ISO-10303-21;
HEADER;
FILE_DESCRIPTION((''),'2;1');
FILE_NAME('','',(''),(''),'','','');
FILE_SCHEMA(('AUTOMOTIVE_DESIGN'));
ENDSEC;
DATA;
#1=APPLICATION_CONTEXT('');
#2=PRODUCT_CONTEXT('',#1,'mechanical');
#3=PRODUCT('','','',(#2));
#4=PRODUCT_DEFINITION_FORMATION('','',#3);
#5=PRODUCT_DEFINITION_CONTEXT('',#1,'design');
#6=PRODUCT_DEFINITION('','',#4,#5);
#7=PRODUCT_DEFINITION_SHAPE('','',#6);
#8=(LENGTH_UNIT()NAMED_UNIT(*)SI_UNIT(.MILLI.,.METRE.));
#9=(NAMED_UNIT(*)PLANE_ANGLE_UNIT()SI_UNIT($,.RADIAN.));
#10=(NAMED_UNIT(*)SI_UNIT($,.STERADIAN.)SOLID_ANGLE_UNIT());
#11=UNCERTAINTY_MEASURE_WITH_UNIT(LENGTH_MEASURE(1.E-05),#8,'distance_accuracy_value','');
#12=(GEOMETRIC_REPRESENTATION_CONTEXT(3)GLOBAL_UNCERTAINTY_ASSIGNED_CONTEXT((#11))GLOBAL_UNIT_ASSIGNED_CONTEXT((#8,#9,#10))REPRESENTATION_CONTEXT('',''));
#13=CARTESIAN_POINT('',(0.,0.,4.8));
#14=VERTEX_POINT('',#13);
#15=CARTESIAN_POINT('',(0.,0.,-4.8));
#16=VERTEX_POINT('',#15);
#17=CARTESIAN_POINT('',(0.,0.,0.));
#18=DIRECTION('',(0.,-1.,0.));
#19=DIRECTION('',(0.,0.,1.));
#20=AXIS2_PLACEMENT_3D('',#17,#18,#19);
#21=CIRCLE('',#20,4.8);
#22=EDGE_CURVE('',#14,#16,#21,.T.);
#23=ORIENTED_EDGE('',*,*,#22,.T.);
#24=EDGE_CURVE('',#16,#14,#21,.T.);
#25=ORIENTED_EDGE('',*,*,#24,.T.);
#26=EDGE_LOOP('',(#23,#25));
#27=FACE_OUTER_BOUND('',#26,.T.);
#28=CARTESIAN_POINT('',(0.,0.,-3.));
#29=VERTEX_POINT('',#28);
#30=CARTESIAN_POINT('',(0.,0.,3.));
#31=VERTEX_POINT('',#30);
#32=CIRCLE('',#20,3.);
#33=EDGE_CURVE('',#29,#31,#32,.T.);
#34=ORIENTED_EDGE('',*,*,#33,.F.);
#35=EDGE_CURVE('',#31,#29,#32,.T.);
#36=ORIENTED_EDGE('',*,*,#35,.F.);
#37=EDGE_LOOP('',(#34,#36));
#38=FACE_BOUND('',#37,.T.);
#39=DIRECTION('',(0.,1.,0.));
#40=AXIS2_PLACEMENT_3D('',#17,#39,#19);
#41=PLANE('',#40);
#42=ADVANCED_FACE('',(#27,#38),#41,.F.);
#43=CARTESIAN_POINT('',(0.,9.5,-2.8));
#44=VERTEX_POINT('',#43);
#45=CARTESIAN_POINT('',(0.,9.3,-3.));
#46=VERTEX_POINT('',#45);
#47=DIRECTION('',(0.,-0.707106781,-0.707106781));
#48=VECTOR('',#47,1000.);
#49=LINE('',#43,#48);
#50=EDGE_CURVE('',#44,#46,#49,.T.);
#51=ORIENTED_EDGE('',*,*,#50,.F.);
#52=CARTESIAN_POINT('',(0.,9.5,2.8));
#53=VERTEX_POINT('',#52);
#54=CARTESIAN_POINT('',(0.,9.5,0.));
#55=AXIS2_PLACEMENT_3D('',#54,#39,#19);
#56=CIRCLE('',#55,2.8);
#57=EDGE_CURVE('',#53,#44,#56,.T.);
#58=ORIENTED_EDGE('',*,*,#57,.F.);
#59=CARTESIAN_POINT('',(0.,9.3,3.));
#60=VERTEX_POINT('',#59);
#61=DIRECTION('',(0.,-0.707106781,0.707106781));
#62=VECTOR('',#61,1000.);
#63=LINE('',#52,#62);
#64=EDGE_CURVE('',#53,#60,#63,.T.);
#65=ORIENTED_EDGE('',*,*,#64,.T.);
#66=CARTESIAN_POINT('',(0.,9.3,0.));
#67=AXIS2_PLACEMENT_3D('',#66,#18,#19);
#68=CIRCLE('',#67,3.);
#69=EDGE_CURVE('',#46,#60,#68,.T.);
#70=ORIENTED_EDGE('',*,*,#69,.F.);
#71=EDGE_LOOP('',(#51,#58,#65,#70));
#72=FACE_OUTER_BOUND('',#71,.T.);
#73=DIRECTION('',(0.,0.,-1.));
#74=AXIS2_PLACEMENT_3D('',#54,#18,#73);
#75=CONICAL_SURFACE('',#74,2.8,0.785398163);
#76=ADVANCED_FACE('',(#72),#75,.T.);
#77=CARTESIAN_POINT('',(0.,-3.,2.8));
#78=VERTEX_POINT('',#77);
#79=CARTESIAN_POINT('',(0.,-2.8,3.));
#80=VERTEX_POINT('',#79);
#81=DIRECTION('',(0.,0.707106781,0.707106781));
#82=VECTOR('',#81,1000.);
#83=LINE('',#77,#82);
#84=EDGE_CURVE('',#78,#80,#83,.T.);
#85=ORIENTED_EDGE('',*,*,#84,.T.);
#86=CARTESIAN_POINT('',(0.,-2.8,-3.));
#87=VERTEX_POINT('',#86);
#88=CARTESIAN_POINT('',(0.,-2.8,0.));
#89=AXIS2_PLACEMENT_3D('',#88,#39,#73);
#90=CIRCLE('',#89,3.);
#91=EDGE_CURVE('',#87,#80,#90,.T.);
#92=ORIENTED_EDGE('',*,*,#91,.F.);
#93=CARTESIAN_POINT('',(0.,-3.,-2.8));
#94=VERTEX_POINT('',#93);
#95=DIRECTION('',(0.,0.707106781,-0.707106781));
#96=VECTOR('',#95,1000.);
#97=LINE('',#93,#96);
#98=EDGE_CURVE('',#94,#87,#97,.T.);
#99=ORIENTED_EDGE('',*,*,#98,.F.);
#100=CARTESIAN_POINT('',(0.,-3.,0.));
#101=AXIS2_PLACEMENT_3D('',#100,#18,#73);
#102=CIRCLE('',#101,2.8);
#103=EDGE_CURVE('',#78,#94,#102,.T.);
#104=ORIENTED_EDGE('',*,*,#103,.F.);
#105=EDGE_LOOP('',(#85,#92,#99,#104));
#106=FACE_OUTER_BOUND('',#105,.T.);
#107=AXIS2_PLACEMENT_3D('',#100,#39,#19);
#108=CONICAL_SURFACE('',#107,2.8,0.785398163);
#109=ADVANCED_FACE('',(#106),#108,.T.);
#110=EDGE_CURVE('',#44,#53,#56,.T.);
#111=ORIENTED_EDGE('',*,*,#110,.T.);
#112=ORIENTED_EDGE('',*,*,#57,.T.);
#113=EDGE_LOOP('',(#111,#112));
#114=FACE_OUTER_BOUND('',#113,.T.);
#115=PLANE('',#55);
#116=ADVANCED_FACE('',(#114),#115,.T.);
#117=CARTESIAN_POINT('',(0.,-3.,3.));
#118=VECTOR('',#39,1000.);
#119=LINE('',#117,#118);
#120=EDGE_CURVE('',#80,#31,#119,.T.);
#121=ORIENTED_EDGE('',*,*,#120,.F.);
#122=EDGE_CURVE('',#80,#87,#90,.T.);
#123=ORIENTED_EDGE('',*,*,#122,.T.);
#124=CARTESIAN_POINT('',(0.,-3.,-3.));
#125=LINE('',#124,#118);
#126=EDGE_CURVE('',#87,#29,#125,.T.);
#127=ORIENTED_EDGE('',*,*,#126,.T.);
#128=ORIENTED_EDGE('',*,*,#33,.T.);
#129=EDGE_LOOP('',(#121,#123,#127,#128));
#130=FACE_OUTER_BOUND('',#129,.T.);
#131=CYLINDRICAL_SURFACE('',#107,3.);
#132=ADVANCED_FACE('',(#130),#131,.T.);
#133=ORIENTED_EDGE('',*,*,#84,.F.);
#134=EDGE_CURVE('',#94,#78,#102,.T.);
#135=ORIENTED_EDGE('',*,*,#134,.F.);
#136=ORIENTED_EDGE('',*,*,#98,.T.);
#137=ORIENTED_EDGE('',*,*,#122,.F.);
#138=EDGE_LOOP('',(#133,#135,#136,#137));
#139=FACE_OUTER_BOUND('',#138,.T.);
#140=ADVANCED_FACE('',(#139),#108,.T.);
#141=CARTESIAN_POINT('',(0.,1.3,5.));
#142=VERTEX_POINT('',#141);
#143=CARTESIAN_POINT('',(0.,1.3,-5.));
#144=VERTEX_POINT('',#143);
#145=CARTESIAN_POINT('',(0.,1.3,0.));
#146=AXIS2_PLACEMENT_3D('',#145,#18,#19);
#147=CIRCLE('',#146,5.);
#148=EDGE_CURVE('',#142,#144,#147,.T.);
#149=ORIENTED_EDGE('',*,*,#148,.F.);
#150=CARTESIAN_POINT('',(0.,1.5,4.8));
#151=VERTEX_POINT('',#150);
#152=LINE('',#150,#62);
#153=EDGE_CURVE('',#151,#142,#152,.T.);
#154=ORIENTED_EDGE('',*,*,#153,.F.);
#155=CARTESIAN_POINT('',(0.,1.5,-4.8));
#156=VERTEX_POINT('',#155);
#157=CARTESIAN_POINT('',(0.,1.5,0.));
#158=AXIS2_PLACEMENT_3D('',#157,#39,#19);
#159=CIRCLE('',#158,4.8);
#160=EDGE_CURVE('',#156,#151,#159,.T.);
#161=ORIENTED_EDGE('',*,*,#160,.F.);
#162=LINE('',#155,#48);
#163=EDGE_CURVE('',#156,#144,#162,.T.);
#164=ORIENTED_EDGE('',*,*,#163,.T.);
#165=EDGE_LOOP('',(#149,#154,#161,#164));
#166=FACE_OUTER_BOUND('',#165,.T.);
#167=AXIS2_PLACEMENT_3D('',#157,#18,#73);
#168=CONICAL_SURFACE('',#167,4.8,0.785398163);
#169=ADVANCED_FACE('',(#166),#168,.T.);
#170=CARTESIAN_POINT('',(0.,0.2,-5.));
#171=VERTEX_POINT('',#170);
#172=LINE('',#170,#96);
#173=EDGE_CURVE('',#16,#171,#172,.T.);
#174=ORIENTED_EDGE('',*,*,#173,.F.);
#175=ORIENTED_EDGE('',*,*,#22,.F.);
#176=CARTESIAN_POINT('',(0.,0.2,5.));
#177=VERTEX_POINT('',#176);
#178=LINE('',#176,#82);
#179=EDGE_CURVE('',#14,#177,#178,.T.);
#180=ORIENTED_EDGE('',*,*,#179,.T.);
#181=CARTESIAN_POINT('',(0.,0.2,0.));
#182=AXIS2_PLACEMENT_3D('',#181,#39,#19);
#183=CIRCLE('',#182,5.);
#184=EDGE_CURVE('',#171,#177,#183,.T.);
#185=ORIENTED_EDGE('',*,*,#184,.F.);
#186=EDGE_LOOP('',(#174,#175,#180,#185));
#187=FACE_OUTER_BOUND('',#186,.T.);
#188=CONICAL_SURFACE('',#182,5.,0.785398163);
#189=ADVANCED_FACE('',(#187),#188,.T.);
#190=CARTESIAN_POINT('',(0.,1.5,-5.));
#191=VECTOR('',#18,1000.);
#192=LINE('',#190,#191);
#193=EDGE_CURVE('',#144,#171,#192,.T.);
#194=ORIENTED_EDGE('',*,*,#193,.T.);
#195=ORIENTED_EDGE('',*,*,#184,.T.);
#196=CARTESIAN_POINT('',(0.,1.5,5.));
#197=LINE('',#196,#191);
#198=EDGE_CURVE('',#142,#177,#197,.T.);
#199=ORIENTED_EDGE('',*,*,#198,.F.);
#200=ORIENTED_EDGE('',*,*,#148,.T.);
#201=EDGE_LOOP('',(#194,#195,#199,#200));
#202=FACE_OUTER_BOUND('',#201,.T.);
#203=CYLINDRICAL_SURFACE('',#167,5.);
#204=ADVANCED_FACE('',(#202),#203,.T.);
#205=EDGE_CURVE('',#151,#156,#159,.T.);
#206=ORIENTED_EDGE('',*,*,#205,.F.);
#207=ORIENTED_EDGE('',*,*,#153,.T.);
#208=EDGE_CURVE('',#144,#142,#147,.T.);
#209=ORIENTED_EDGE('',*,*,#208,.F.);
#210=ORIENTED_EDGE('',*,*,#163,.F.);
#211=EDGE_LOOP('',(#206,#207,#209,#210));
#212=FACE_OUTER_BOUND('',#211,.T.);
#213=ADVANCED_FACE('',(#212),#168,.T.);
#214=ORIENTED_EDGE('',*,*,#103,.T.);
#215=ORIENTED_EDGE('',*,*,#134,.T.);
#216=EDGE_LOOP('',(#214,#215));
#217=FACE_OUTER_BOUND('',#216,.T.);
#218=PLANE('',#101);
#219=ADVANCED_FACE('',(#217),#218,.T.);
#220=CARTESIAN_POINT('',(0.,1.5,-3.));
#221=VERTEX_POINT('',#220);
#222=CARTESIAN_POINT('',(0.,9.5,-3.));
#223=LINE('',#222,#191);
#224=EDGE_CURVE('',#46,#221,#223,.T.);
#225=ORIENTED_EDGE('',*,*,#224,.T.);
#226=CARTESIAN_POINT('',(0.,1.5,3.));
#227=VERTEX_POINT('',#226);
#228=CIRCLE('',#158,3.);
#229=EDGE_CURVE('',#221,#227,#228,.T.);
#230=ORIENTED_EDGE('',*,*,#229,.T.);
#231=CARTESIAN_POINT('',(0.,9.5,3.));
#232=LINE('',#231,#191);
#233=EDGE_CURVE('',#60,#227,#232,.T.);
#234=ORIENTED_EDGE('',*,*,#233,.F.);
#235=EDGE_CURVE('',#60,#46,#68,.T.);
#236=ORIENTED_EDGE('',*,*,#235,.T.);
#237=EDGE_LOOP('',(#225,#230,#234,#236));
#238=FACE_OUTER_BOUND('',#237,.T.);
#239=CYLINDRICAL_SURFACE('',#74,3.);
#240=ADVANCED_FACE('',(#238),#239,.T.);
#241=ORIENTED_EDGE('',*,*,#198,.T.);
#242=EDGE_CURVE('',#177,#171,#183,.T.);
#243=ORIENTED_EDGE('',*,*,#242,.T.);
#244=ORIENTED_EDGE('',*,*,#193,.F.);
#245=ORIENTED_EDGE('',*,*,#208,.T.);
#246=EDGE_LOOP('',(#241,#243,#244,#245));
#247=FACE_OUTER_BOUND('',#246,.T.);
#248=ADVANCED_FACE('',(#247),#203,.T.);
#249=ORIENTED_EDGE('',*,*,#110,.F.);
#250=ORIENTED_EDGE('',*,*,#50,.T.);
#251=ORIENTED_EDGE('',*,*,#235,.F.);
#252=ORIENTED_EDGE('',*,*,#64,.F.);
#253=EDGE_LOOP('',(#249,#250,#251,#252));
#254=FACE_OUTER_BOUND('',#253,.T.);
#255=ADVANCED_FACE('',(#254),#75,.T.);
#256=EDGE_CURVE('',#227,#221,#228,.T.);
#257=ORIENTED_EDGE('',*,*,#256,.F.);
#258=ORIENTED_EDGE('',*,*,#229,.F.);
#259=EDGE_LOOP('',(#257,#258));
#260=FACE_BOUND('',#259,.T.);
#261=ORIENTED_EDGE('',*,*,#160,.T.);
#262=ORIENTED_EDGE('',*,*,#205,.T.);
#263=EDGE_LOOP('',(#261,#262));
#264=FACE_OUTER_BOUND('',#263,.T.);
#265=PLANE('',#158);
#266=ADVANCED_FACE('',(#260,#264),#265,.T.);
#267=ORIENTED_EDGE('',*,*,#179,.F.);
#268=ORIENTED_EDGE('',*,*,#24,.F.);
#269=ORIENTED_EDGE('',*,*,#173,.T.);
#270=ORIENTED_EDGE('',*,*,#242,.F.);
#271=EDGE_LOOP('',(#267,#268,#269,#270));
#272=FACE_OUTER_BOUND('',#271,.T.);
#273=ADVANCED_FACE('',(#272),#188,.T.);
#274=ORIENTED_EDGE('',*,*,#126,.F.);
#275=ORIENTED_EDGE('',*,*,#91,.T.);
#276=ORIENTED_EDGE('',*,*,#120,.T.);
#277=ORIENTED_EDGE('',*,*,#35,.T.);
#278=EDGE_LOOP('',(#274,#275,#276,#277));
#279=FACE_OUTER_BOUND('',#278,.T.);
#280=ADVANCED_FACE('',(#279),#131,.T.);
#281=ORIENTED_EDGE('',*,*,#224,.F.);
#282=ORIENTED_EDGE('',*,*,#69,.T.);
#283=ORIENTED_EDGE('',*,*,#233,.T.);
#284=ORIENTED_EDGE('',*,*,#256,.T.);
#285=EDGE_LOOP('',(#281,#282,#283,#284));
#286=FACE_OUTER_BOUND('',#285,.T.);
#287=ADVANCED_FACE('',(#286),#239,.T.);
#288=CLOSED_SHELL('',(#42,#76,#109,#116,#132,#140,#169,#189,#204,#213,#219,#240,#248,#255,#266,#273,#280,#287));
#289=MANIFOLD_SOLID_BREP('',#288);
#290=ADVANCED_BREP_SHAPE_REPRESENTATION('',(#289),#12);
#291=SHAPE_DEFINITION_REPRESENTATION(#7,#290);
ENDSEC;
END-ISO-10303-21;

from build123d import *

# Parameters (mm, degrees)
SKETCH1_R           = 5
BOSS_EXTRUDE1_DEPTH = 1.5
SKETCH2_R           = 3
BOSS_EXTRUDE2_DEPTH = 8
BOSS_EXTRUDE3_START = 3
SKETCH3_R           = 3
BOSS_EXTRUDE3_DEPTH = 3
CHAMFER1_SIZE       = 0.2


with BuildPart() as part:
    # Sketch1 → Boss-Extrude1 (new body)
    with BuildSketch(Plane(origin=(0, 0, 0), x_dir=(1, 0, 0), z_dir=(0, 1, 0))):
        with Locations(Location((0, 0, 0), (0, 0, 270))):
            Circle(SKETCH1_R)
    extrude(amount=BOSS_EXTRUDE1_DEPTH)

    # Sketch2 → Boss-Extrude2 (add)
    with BuildSketch(Plane(origin=(0, 1.5, 0), x_dir=(1, 0, 0), z_dir=(0, 1, 0))):
        with Locations(Location((0, 0, 0), (0, 0, 270))):
            Circle(SKETCH2_R)
    extrude(amount=BOSS_EXTRUDE2_DEPTH)

    # Sketch3 → Boss-Extrude3 (add)
    with BuildSketch(Plane.XZ.offset(BOSS_EXTRUDE3_START)):
        with Locations(Location((0, 0, 0), (0, 0, 90))):
            Circle(SKETCH3_R)
    extrude(amount=-BOSS_EXTRUDE3_DEPTH)

    # Chamfer1
    chamfer1_edges = [part.edges().sort_by_distance(p)[0] for p in [
        (0, -3, -3),
        (0, 0, -5),
        (0, 1.5, -5),
        (0, 9.5, -3),
    ]]
    chamfer(chamfer1_edges, length=CHAMFER1_SIZE)


solid = part.part
